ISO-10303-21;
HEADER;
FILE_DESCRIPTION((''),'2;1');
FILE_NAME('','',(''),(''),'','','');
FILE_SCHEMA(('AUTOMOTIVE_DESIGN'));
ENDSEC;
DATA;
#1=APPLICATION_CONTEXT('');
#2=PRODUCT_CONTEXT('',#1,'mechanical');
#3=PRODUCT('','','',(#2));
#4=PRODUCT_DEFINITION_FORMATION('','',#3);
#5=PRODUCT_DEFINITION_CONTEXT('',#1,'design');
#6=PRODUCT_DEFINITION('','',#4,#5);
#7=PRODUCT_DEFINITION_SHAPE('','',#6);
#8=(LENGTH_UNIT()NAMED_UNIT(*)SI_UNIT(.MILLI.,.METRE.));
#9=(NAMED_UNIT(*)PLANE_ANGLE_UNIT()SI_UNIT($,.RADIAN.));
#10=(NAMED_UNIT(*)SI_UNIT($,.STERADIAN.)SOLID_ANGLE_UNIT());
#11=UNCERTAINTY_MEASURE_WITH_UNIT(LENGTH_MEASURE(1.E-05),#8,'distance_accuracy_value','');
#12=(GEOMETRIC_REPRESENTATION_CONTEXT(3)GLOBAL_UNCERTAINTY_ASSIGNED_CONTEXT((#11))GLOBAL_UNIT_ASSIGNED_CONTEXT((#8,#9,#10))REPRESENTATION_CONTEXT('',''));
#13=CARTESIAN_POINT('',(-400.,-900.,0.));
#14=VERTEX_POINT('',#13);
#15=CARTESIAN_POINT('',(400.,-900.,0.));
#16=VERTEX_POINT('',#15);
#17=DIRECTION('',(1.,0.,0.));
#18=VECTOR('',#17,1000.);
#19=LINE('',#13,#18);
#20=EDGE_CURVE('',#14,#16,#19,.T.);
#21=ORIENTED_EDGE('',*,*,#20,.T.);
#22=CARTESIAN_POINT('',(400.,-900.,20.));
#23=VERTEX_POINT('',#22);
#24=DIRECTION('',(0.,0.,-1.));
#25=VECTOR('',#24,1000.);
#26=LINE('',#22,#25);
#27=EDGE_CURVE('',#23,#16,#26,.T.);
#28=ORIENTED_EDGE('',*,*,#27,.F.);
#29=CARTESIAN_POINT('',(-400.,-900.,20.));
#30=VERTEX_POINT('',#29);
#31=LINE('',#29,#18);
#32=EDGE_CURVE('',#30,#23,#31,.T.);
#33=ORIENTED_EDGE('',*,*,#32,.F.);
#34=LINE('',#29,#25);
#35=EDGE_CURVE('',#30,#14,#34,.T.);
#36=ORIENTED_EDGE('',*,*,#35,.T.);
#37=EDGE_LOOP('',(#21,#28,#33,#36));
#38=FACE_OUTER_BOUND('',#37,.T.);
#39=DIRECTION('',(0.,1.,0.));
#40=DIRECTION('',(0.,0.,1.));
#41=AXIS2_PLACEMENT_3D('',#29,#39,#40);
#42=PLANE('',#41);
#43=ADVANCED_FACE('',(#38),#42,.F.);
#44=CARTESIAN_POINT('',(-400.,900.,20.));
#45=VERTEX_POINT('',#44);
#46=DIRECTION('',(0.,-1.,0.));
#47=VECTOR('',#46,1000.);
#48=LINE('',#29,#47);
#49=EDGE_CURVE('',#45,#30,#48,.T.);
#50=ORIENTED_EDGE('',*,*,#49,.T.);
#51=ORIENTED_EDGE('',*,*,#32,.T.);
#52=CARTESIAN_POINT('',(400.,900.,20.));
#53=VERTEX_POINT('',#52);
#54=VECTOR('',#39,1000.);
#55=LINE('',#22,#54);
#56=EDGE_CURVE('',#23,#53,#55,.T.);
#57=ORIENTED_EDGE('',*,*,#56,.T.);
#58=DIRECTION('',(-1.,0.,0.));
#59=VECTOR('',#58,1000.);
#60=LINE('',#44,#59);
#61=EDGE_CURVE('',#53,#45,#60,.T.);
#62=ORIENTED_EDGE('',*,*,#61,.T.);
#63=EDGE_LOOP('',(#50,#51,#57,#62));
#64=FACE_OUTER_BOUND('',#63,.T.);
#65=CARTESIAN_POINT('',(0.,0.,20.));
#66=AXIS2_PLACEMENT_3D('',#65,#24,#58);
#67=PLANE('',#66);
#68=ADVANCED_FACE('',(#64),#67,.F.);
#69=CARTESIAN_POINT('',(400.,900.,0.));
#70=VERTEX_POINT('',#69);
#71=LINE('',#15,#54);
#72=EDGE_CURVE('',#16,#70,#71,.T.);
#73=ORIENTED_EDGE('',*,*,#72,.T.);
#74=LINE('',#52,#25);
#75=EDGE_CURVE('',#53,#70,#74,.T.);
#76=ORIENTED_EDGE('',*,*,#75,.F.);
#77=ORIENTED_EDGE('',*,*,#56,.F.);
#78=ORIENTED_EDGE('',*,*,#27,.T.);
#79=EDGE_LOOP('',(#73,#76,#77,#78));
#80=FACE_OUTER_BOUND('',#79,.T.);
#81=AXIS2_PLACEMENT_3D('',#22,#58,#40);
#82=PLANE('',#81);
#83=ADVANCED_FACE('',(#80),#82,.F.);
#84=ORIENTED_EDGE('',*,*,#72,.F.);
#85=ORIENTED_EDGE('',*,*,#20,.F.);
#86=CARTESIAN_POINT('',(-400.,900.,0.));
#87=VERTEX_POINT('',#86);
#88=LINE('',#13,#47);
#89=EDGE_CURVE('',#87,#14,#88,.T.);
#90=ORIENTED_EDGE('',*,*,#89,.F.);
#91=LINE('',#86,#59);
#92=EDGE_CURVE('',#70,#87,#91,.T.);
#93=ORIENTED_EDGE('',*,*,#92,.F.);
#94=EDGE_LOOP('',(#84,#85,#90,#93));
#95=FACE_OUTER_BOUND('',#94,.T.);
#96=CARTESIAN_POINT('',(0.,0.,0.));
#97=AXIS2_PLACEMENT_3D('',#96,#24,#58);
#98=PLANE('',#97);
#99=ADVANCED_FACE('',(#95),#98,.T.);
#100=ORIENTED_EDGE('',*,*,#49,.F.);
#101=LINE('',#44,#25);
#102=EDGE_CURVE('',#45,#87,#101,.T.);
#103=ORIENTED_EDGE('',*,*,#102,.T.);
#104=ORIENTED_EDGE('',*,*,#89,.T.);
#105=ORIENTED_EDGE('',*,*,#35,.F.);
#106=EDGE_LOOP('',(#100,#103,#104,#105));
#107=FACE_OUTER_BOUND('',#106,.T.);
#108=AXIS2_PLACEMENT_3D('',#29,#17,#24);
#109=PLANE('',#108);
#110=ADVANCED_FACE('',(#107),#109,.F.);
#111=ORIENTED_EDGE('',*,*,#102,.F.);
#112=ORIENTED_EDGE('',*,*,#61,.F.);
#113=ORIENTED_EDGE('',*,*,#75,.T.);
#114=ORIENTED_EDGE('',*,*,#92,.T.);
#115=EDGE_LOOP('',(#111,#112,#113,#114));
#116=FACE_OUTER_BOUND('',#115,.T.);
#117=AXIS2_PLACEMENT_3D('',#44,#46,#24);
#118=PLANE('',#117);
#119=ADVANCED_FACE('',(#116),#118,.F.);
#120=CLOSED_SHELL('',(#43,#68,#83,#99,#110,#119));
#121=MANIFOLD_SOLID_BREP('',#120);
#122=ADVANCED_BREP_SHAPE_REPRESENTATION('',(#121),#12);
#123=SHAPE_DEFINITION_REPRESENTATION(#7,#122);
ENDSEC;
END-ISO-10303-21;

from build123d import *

# Parameters (mm, degrees)
SKETCH_1_W      = 800
SKETCH_1_H      = 1800
EXTRUDE_1_DEPTH = 20


with BuildPart() as part:
    # 草图1 → 凸台-拉伸1 (new body)
    with BuildSketch(Plane.XY):
        Rectangle(SKETCH_1_W, SKETCH_1_H)
    extrude(amount=EXTRUDE_1_DEPTH)


solid = part.part
